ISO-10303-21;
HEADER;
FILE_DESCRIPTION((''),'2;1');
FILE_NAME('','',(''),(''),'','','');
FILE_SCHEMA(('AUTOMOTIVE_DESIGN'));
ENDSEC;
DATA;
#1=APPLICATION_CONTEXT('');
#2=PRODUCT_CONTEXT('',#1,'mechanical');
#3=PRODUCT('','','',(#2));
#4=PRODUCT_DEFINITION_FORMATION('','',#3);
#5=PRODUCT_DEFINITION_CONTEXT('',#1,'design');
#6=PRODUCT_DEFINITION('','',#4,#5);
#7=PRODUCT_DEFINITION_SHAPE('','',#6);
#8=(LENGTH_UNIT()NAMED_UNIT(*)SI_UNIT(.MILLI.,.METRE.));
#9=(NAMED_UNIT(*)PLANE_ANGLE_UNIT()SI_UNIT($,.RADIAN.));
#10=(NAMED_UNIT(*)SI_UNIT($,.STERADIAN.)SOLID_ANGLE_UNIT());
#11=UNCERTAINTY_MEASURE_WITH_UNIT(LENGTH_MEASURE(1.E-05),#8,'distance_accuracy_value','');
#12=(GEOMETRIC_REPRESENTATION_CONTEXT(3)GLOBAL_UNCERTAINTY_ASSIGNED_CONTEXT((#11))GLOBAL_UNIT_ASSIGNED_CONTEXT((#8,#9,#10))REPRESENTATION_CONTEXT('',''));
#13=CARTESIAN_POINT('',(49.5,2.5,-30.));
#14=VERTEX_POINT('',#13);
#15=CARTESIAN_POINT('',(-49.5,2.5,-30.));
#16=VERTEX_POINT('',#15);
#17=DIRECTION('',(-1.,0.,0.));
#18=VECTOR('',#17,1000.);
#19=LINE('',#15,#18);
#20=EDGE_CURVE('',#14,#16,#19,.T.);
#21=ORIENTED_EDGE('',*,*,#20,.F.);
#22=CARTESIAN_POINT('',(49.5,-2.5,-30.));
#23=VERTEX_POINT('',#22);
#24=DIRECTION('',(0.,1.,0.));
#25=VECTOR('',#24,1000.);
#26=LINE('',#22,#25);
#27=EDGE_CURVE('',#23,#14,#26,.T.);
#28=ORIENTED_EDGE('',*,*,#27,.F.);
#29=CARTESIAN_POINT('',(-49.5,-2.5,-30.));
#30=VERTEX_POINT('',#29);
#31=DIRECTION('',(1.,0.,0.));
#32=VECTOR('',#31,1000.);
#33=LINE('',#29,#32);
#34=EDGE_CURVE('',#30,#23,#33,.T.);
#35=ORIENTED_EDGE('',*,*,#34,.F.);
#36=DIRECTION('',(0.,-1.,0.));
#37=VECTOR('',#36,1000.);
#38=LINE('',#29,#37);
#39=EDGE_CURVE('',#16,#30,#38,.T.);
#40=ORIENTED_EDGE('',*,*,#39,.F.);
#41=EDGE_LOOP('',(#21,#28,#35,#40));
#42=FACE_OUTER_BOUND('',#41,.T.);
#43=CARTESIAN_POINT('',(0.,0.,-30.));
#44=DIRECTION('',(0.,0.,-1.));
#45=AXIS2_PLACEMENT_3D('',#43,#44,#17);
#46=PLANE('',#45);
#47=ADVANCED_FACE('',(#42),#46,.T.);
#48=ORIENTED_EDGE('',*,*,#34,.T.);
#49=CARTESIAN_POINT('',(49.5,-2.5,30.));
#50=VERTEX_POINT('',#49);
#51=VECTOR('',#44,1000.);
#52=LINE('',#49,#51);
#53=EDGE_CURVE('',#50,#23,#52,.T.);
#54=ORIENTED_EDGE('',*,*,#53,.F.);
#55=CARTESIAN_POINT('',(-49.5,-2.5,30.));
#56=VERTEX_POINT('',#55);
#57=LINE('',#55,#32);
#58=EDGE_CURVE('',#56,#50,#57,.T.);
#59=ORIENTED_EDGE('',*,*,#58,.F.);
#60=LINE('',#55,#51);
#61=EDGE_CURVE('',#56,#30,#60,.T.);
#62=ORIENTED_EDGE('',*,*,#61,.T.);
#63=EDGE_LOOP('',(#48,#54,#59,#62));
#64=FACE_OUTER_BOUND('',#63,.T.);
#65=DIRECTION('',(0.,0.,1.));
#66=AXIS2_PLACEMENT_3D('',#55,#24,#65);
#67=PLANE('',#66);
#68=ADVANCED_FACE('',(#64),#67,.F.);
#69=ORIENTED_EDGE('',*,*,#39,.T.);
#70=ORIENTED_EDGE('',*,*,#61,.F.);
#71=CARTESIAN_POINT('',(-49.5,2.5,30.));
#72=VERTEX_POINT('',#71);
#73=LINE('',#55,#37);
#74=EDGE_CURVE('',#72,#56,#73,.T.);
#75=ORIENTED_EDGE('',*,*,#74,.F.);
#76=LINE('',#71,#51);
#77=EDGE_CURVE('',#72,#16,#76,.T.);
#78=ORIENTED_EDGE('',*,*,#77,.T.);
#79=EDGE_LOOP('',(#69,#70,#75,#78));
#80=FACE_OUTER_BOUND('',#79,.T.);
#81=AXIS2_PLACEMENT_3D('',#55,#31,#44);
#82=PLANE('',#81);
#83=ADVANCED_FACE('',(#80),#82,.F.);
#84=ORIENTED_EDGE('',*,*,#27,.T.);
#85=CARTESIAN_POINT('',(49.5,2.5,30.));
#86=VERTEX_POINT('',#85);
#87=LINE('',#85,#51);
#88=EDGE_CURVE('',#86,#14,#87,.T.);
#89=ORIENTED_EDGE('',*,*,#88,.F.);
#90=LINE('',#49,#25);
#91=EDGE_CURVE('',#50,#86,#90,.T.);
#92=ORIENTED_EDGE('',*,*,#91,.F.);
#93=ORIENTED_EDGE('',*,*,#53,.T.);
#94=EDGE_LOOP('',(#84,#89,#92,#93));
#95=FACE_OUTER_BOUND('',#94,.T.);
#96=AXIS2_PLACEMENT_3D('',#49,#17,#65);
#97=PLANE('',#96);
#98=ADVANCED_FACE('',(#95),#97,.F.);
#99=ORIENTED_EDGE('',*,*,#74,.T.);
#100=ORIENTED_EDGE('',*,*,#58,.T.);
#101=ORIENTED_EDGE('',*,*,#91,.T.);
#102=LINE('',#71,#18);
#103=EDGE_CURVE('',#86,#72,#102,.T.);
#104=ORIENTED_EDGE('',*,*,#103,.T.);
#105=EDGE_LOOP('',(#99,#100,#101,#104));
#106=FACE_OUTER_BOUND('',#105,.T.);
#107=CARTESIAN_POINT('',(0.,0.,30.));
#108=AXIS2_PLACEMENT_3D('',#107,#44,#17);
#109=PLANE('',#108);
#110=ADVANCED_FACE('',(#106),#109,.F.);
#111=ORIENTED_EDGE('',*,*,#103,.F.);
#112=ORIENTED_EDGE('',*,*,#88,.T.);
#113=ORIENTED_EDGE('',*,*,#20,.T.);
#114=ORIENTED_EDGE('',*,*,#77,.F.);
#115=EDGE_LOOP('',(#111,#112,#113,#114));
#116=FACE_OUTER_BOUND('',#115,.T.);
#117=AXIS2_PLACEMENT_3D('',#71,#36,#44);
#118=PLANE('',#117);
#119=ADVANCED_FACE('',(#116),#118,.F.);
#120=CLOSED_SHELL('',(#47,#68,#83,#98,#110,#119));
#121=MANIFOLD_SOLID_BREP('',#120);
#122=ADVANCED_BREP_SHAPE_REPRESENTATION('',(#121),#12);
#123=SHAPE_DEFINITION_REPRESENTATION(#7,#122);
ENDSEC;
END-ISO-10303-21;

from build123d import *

# Parameters (mm, degrees)
SKETCH_1_W      = 99
SKETCH_1_H      = 5
EXTRUDE_1_DEPTH = 30


with BuildPart() as part:
    # 草图1 → 凸台-拉伸1 (new, symmetric)
    with BuildSketch(Plane.XY):
        Rectangle(SKETCH_1_W, SKETCH_1_H)
    extrude(amount=EXTRUDE_1_DEPTH, both=True)


solid = part.part
